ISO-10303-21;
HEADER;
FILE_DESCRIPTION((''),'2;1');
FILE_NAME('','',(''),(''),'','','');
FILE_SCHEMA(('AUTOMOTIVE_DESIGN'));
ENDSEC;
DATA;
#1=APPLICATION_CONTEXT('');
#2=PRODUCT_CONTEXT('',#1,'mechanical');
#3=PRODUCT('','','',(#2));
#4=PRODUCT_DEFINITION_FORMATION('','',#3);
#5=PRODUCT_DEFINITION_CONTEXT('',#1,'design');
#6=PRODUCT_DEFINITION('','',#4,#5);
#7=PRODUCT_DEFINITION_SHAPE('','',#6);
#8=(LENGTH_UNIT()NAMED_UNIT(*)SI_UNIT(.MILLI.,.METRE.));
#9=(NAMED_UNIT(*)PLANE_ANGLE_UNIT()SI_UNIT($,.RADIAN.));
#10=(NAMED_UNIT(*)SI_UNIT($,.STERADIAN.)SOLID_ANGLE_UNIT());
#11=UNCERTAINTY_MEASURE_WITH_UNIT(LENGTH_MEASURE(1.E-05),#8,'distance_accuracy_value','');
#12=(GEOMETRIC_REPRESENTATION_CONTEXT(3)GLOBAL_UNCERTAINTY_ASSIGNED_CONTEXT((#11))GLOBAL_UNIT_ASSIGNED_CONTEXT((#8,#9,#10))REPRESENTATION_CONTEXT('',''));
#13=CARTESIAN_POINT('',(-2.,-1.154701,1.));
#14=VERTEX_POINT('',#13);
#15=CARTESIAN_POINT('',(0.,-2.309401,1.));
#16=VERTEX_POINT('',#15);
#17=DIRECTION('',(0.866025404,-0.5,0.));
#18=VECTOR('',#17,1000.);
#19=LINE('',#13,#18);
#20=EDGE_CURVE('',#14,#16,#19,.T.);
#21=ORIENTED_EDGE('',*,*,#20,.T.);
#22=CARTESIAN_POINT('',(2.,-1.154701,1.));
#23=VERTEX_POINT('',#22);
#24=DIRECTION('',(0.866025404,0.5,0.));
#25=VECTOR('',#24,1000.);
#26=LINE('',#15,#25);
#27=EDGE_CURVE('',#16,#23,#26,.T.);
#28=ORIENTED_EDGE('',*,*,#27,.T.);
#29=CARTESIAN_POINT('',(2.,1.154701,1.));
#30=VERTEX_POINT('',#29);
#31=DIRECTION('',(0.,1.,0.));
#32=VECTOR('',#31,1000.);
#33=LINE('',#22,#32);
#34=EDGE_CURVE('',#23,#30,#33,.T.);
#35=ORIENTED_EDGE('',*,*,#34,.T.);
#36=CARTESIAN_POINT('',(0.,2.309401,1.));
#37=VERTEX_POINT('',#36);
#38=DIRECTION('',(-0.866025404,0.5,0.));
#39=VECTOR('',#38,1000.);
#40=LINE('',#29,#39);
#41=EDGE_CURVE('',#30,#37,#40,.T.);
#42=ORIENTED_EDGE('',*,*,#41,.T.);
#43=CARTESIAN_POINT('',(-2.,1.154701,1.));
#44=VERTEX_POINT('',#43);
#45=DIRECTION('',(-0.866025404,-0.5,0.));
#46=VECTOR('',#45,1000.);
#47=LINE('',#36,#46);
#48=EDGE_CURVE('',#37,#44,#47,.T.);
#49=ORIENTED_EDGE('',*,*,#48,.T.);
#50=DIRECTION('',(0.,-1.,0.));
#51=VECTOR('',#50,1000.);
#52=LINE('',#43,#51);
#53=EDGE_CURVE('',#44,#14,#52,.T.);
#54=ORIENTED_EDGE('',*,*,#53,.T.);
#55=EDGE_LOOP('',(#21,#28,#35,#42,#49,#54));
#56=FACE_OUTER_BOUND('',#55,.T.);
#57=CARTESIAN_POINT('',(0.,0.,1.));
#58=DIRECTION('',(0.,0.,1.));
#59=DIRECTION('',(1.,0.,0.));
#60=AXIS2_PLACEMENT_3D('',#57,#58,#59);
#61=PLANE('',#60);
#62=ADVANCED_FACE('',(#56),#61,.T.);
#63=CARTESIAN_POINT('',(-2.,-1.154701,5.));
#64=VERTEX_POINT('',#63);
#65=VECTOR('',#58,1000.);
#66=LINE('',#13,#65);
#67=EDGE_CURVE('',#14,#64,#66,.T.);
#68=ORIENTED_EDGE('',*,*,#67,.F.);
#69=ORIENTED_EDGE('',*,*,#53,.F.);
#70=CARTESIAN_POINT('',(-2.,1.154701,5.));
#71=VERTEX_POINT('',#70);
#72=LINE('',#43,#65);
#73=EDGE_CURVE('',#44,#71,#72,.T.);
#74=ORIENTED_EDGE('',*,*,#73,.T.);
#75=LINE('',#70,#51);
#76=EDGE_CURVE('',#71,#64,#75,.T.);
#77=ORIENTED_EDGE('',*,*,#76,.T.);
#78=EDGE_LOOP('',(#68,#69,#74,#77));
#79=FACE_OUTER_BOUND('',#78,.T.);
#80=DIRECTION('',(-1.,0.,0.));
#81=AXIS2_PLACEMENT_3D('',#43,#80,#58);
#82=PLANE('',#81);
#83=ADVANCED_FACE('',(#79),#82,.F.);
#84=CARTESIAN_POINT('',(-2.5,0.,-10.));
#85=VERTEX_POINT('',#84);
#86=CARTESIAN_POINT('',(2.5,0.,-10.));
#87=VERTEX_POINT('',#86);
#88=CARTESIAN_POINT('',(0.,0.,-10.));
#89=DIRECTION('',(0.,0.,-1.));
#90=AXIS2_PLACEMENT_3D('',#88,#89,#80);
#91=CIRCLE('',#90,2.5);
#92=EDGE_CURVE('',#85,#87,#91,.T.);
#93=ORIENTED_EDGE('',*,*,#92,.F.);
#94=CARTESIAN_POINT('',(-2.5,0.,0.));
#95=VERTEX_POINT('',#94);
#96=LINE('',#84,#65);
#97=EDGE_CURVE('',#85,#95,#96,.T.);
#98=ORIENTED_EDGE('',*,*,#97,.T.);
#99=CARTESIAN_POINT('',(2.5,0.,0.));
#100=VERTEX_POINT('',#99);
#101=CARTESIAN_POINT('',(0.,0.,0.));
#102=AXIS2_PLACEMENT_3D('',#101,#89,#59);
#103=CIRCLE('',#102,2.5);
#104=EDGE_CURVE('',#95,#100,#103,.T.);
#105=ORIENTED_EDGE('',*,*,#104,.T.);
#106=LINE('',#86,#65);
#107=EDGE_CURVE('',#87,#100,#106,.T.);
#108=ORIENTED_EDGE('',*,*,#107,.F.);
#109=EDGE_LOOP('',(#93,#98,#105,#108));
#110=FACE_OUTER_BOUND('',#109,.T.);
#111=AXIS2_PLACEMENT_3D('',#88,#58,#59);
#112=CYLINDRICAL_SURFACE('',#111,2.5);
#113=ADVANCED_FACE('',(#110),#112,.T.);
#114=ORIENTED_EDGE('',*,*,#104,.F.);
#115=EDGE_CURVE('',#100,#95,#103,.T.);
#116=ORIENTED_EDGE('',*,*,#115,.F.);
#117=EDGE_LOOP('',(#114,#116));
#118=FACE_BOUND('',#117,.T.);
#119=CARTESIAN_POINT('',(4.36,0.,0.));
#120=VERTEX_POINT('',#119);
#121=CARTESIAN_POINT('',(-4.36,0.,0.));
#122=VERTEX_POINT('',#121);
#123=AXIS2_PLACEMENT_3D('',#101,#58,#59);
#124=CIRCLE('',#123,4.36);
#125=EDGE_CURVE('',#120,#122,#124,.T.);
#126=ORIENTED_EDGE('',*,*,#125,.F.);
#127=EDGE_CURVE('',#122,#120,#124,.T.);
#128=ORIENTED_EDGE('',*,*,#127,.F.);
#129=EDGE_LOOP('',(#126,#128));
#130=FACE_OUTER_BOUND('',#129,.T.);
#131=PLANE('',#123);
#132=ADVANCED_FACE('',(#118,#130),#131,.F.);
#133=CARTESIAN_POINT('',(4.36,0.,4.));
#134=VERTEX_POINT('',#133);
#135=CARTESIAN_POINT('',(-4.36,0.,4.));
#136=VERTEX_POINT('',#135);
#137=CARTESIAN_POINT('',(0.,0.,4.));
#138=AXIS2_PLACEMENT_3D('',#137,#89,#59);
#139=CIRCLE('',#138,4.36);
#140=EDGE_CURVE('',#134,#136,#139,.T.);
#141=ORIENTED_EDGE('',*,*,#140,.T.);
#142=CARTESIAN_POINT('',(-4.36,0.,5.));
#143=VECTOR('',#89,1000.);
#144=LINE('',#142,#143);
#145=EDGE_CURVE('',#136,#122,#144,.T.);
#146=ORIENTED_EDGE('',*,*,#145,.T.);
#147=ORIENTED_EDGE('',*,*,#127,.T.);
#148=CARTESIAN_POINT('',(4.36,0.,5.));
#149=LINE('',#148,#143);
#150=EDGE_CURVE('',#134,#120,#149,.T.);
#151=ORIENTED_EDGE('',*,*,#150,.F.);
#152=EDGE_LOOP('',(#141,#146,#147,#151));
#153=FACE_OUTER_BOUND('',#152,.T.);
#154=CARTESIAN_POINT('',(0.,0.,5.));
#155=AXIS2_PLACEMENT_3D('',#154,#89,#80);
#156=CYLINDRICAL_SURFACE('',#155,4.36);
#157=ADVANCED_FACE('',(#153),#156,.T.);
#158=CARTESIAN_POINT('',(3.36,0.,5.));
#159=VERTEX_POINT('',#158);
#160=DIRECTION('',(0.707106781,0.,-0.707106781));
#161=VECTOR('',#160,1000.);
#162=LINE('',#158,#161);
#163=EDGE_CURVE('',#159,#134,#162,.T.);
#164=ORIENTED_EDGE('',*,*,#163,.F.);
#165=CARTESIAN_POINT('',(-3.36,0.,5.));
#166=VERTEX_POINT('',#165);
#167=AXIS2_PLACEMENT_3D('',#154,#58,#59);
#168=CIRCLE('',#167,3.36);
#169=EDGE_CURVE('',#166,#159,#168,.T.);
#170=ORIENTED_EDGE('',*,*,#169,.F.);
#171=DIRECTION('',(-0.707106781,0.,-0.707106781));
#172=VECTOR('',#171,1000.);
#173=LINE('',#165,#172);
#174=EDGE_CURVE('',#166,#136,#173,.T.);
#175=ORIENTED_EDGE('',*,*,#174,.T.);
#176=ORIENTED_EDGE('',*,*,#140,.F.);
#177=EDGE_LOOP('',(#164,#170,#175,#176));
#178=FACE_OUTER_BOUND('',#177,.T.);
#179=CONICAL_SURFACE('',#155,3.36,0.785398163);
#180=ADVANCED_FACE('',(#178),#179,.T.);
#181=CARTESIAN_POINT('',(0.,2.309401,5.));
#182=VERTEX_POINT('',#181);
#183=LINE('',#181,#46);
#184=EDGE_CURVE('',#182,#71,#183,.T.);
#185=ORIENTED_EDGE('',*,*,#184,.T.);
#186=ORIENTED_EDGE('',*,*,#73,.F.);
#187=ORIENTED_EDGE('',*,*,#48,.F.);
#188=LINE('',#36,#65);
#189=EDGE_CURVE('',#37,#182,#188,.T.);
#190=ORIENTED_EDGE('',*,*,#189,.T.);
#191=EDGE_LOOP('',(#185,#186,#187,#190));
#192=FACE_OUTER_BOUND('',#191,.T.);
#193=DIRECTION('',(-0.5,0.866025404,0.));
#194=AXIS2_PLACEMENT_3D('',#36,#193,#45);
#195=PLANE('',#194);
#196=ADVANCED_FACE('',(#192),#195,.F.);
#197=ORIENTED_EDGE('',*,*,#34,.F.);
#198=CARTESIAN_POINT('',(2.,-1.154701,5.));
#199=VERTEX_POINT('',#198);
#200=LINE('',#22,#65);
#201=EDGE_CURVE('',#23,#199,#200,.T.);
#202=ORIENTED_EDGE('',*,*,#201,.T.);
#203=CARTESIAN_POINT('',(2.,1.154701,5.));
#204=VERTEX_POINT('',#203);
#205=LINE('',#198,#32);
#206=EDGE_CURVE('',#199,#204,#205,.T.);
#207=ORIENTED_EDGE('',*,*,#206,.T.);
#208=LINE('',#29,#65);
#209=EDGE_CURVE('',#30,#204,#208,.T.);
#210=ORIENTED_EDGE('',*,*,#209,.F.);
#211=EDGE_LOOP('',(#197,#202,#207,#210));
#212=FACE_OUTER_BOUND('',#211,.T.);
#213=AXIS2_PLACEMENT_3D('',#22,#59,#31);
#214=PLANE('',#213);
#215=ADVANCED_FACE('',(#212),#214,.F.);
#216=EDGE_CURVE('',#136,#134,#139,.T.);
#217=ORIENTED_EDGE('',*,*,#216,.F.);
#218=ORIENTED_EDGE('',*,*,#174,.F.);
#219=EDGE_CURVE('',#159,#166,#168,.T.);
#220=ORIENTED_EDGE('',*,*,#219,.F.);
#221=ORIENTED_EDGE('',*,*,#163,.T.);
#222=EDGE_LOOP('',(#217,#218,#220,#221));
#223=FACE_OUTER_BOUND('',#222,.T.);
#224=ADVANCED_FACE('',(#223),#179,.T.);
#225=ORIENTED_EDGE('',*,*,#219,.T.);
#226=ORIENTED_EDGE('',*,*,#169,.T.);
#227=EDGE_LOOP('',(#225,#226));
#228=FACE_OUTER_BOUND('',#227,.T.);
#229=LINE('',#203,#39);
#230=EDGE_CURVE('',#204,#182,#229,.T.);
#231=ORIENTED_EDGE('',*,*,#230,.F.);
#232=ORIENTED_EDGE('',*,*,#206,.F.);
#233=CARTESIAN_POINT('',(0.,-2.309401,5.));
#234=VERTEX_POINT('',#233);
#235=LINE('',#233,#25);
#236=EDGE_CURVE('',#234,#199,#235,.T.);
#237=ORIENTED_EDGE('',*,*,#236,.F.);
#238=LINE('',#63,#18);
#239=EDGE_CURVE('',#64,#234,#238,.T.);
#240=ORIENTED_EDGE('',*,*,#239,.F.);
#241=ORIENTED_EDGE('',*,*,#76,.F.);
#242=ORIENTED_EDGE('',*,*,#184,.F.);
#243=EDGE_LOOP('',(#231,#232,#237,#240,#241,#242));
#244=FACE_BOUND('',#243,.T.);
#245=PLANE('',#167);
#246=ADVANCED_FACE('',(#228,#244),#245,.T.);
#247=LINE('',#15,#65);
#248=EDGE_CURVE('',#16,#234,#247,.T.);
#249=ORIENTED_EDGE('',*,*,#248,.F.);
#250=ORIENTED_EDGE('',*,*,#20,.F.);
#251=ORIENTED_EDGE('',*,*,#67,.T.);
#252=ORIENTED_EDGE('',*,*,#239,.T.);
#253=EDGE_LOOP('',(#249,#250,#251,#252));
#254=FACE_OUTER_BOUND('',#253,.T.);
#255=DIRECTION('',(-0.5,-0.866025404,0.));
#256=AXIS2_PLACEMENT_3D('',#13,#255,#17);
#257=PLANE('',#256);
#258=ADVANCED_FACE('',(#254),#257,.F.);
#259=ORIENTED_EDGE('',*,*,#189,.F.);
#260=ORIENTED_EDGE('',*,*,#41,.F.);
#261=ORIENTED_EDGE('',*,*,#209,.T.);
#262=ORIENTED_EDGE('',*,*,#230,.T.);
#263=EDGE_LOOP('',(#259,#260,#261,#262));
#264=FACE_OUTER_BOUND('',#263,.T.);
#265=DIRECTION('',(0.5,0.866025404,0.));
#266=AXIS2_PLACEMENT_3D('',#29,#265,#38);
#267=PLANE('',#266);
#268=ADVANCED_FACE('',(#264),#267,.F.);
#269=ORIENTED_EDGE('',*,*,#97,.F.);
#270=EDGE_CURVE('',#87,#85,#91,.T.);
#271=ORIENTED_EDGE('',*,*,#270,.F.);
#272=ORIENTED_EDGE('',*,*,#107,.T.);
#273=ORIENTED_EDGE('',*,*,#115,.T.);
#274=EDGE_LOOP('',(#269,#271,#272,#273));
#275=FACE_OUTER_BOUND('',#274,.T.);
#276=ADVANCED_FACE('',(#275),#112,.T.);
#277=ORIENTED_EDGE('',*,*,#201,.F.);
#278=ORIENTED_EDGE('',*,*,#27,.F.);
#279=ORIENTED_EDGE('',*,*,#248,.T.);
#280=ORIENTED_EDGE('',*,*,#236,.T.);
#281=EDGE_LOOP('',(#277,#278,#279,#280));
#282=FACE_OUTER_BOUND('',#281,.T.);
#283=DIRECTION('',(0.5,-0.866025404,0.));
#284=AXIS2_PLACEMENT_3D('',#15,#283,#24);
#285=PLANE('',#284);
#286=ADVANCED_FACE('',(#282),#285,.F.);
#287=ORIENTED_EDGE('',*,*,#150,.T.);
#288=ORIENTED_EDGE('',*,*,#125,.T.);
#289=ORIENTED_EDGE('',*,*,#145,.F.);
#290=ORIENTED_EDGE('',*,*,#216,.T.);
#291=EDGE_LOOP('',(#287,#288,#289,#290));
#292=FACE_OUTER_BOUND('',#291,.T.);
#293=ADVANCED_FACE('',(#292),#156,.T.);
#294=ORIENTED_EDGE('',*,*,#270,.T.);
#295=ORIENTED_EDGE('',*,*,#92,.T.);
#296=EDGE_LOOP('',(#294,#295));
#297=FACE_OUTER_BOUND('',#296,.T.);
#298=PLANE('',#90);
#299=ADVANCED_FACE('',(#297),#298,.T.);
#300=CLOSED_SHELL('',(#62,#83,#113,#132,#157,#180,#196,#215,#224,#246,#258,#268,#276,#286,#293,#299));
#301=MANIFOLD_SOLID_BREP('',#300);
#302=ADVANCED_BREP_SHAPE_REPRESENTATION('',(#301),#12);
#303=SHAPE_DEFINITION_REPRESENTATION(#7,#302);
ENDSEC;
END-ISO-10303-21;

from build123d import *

# Parameters (mm, degrees)
SKETCH_1_R          = 4.36
EXTRUDE_1_DEPTH     = 5
CUT_EXTRUDE_1_DEPTH = 4
CHAMFER_1_SIZE      = 1
SKETCH_3_R          = 2.5
EXTRUDE_2_DEPTH     = 10


with BuildPart() as part:
    # 草图1 → 凸台-拉伸1 (new body)
    with BuildSketch(Plane.XY):
        Circle(SKETCH_1_R)
    extrude(amount=EXTRUDE_1_DEPTH)

    # 草图2 → 切除-拉伸1 (cut)
    with BuildSketch(Plane.XY.offset(5)):
        Polygon((0, 2.309401077), (-2, 1.154700538), (-2, -1.154700538), (0, -2.309401077), (2, -1.154700538), (2, 1.154700538), align=None)
    extrude(amount=-CUT_EXTRUDE_1_DEPTH, mode=Mode.SUBTRACT)

    # 倒角1
    chamfer_1_edges = [part.edges().sort_by_distance(p)[0] for p in [
        (-4.36, 0, 5),
    ]]
    chamfer(chamfer_1_edges, length=CHAMFER_1_SIZE)

    # 草图3 → 凸台-拉伸2 (add)
    with BuildSketch(Plane(origin=(0, 0, 0), x_dir=(-1, 0, 0), z_dir=(0, 0, -1))):
        with Locations(Location((0, 0, 0), (0, 0, 180))):
            Circle(SKETCH_3_R)
    extrude(amount=EXTRUDE_2_DEPTH)


solid = part.part
